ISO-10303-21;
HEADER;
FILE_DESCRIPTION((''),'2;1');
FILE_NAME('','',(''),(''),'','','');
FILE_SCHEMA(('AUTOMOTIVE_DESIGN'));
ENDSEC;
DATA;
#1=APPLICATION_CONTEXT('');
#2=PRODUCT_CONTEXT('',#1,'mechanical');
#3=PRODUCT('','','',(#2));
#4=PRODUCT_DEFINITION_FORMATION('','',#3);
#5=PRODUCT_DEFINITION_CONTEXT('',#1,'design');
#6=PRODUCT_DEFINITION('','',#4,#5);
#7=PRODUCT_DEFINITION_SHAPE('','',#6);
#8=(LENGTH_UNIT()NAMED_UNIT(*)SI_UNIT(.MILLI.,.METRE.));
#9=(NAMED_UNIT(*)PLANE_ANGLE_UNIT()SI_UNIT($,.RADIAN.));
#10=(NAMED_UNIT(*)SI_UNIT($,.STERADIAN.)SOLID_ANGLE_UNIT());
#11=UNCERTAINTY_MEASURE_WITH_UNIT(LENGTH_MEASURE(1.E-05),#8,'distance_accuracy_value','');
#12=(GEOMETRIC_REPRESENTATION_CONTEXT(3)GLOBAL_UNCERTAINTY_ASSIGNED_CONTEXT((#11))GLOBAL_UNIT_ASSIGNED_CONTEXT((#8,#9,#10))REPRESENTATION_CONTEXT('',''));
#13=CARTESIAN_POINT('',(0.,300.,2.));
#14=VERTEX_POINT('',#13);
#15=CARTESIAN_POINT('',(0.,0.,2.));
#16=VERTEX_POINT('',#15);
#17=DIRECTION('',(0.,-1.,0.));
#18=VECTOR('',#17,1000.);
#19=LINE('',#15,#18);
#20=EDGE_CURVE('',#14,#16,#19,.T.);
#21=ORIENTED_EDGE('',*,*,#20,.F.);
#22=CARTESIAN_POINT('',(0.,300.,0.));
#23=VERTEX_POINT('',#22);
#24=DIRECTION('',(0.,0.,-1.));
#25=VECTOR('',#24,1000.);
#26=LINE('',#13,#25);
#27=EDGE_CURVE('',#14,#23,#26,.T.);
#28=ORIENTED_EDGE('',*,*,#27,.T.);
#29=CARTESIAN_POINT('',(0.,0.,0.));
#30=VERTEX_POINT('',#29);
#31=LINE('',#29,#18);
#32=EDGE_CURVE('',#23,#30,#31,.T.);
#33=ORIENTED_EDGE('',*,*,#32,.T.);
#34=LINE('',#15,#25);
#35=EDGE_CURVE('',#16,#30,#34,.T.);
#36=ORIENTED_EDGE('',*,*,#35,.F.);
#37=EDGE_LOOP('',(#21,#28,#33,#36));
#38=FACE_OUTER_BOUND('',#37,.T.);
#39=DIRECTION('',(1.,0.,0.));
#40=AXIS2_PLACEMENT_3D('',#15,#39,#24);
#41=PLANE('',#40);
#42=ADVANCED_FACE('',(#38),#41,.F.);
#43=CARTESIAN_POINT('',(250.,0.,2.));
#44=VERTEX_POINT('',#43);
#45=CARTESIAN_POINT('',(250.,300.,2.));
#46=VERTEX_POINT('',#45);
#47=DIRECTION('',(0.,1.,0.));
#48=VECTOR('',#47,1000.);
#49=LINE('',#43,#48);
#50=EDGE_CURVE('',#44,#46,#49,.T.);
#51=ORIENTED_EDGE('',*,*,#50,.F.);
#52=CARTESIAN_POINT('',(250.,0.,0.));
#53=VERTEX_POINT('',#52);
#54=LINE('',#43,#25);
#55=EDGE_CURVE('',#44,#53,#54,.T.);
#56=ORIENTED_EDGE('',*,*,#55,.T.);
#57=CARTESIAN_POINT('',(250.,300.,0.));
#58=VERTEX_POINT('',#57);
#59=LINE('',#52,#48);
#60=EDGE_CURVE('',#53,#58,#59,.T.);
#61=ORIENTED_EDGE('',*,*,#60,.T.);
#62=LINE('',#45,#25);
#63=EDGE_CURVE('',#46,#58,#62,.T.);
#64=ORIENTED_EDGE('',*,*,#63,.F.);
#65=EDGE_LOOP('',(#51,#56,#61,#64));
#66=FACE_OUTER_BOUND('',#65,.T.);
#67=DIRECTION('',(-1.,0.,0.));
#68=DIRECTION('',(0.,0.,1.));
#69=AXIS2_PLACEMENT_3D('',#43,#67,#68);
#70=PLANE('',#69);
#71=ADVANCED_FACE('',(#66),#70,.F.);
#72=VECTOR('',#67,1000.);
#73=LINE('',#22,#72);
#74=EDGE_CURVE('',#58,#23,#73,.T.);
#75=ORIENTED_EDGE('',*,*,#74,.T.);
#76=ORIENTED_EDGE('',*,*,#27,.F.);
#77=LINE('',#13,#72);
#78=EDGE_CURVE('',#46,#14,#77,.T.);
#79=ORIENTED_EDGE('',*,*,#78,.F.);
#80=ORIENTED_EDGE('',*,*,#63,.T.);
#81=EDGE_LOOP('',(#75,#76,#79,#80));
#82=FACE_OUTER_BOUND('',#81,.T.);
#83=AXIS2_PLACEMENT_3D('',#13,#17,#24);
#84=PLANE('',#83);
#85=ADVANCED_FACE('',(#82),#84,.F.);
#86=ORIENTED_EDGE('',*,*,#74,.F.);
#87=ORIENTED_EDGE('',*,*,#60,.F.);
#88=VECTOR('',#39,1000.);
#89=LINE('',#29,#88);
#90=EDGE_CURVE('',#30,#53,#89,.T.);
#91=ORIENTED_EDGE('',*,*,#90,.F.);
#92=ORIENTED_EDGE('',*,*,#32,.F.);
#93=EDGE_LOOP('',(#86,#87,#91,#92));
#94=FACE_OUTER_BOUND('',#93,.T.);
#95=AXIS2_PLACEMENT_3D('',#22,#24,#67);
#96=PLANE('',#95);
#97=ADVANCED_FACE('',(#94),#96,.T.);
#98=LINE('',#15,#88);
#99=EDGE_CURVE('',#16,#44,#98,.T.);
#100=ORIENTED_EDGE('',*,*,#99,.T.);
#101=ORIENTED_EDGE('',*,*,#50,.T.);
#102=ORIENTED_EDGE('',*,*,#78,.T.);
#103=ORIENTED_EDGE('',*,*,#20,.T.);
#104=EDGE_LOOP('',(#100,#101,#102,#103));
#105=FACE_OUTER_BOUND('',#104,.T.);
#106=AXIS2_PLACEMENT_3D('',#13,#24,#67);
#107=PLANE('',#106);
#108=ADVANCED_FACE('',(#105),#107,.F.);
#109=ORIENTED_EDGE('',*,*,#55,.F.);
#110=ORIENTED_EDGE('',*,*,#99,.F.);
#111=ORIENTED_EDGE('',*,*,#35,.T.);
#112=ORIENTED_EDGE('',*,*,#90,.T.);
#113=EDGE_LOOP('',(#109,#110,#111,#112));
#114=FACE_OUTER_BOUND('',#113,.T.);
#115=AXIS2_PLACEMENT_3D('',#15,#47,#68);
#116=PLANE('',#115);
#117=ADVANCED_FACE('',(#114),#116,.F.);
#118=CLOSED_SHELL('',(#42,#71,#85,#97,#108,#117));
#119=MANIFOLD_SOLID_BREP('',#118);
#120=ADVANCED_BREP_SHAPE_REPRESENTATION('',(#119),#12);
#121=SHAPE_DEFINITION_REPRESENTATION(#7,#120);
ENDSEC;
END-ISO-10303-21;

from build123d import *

# Parameters (mm, degrees)
SKETCH1_W           = 250
SKETCH1_H           = 300
BOSS_EXTRUDE1_DEPTH = 2


with BuildPart() as part:
    # Sketch1 → Boss-Extrude1 (new body)
    with BuildSketch(Plane.XY):
        with Locations((125, 150)):
            Rectangle(SKETCH1_W, SKETCH1_H)
    extrude(amount=BOSS_EXTRUDE1_DEPTH)


solid = part.part
